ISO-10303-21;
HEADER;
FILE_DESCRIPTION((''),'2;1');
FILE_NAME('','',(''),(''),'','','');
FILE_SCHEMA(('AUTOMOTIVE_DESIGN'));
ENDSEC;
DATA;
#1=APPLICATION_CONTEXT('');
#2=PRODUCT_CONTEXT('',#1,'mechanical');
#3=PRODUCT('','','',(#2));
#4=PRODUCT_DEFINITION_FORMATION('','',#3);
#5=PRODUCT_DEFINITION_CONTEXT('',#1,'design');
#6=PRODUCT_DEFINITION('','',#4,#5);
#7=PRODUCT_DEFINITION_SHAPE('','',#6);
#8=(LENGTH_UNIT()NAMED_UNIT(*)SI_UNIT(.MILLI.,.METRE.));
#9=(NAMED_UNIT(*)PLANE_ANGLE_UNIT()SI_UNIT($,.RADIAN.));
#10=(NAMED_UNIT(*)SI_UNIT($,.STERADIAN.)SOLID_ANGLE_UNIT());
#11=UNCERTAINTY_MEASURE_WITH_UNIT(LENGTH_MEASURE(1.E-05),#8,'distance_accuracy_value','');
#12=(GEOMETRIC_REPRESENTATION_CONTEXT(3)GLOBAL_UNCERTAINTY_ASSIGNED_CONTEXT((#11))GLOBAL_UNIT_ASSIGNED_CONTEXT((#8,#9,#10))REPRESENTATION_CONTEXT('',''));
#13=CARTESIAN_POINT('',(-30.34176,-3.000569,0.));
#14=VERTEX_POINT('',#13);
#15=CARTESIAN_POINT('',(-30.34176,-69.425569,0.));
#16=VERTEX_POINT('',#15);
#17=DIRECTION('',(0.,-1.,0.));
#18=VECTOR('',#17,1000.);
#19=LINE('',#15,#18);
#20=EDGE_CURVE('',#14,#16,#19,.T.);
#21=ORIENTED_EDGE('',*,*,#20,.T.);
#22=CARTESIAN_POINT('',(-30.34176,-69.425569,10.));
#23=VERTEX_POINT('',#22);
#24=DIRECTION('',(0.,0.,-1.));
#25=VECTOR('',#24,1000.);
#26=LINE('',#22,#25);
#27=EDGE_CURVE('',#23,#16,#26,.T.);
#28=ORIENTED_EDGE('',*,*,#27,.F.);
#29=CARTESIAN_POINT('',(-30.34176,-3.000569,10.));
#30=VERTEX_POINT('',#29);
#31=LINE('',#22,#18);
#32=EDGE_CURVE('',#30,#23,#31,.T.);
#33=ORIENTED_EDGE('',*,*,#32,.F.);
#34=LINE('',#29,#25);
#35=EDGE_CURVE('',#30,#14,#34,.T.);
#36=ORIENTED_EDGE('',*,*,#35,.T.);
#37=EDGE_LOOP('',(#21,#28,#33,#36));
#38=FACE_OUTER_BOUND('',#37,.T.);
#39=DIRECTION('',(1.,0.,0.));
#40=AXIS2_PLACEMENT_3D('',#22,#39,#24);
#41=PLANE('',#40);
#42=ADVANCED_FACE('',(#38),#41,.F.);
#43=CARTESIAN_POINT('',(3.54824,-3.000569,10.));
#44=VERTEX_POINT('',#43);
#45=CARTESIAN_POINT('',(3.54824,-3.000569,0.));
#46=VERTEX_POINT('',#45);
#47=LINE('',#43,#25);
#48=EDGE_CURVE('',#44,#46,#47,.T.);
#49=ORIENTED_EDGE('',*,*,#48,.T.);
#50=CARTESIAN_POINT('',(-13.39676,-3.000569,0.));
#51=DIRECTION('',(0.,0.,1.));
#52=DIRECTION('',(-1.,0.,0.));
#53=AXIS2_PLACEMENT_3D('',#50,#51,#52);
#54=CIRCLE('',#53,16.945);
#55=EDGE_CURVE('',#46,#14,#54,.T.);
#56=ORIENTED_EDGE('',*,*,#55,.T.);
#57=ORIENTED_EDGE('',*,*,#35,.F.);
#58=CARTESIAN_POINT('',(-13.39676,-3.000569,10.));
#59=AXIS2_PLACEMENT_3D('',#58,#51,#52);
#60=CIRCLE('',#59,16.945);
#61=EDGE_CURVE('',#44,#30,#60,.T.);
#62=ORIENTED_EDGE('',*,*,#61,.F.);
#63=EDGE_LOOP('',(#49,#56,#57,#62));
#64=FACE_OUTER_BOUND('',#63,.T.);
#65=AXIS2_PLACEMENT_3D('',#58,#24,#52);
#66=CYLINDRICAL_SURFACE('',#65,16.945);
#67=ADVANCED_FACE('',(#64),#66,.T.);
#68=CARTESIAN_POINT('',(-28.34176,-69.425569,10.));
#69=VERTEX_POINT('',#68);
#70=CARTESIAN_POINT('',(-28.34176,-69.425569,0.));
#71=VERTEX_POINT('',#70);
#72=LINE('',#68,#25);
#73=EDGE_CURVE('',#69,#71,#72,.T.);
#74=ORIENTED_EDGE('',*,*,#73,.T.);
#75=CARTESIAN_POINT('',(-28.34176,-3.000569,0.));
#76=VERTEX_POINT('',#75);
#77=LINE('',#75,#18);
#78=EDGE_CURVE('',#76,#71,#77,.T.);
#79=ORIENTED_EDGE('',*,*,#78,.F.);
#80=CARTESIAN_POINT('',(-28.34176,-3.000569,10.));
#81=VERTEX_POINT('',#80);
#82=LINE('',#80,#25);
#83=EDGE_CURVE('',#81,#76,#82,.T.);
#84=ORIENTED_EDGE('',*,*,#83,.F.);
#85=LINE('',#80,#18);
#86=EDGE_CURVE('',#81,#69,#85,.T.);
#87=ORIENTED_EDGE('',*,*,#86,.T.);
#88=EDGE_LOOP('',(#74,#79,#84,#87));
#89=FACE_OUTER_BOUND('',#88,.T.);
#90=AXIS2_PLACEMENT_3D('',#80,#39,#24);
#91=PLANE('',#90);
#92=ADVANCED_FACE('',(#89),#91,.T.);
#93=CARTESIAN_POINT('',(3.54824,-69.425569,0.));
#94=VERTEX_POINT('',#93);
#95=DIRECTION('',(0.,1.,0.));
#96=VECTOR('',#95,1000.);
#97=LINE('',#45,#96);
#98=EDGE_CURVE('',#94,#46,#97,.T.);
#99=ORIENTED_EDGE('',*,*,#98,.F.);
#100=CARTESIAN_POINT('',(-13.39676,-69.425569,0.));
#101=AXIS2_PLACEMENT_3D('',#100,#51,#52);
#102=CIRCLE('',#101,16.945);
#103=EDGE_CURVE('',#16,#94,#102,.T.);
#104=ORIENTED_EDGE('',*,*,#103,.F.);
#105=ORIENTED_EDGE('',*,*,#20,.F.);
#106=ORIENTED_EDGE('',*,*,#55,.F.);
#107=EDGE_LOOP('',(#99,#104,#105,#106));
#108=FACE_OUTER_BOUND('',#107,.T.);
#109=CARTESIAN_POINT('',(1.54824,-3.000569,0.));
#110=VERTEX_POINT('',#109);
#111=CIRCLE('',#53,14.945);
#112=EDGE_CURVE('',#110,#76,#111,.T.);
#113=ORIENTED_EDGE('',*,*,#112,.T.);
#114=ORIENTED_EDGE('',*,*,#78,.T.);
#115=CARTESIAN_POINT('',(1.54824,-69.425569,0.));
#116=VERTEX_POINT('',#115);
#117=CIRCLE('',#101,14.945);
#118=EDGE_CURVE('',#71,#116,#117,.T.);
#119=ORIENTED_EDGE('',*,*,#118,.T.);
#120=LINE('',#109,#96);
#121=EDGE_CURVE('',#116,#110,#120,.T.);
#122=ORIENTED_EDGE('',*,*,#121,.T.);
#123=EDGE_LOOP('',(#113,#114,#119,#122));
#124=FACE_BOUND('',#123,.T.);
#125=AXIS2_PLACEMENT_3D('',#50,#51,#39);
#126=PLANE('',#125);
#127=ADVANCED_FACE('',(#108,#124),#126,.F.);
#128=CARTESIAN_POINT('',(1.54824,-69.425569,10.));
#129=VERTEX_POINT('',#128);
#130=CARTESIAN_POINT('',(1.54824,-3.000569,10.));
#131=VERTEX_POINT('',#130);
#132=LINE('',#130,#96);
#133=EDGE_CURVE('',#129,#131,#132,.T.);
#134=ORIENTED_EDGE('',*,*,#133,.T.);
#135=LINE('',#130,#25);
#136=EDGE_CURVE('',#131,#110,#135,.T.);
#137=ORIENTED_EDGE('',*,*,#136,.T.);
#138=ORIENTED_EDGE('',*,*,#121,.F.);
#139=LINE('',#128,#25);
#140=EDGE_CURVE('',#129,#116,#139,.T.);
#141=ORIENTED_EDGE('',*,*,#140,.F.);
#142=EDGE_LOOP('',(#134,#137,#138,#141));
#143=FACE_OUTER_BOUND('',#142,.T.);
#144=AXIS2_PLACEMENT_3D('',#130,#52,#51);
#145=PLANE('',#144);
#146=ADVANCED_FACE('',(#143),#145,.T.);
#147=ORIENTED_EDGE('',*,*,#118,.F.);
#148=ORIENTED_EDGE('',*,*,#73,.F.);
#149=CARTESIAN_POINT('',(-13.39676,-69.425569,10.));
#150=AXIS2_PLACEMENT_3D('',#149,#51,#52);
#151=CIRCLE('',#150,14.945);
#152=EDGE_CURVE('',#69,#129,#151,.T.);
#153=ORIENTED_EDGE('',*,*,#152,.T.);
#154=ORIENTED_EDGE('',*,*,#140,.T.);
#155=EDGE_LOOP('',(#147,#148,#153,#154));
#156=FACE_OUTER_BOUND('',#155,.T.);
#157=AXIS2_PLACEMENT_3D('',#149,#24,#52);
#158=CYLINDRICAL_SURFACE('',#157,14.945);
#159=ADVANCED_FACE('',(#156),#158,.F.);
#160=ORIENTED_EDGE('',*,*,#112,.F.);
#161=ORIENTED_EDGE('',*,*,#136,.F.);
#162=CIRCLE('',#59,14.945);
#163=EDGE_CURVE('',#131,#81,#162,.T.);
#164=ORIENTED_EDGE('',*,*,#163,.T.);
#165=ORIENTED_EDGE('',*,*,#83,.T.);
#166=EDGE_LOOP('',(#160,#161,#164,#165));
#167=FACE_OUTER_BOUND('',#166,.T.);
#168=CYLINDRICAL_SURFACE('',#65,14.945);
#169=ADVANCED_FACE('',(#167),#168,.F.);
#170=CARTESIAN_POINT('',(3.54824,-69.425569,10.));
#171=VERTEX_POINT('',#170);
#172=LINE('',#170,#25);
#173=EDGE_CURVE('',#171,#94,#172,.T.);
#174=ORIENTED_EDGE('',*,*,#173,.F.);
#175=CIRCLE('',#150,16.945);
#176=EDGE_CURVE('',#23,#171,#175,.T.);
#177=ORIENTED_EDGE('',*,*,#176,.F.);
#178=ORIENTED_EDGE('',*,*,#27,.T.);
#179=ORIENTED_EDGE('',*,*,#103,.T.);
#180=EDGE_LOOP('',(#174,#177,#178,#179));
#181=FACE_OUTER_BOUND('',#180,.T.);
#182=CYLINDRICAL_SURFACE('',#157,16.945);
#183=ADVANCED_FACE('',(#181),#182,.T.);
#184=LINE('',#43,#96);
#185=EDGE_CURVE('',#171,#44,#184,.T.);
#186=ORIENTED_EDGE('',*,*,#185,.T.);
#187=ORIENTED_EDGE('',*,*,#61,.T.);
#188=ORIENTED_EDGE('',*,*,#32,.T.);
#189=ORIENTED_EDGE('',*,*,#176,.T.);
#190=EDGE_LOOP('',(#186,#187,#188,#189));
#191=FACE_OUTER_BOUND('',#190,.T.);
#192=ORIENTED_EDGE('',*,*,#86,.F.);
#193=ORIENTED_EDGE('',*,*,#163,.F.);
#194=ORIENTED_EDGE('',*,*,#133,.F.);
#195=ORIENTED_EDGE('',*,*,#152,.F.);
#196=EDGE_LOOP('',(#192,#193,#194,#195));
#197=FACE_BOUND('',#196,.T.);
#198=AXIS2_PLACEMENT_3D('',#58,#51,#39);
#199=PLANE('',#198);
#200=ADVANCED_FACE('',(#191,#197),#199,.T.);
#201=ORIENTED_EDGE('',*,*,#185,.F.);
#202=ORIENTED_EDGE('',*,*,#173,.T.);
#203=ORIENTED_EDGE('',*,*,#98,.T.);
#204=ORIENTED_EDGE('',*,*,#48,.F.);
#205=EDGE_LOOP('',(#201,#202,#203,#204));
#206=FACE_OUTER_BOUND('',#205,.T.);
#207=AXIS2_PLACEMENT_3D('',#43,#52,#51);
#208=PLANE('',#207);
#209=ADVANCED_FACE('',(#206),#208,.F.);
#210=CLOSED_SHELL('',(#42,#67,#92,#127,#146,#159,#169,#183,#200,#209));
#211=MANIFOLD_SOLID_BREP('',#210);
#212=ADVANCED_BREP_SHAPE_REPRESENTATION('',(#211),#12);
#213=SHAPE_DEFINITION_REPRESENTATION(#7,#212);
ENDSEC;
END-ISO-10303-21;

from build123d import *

# Parameters (mm, degrees)
EXTRUDE_THIN1_DEPTH = 10


with BuildPart() as part:
    # Sketch2 → Extrude-Thin1 (new body)
    with BuildSketch(Plane.XY):
        with BuildLine():
            Line((-30.341760221, -69.425568872), (-30.341760221, -3.000568872))
            ThreePointArc((-30.341760221, -3.000568872), (-13.396760221, 13.944431128), (3.548239779, -3.000568872))
            Line((3.548239779, -3.000568872), (3.548239779, -69.425568872))
            ThreePointArc((3.548239779, -69.425568872), (-13.396760221, -86.370568872), (-30.341760221, -69.425568872))
        make_face()
        with BuildLine():
            Line((-28.341760221, -69.425568872), (-28.341760221, -3.000568872))
            ThreePointArc((-28.341760221, -3.000568872), (-13.396760221, 11.944431128), (1.548239779, -3.000568872))
            Line((1.548239779, -3.000568872), (1.548239779, -69.425568872))
            ThreePointArc((1.548239779, -69.425568872), (-13.396760221, -84.370568872), (-28.341760221, -69.425568872))
        make_face(mode=Mode.SUBTRACT)
    extrude(amount=EXTRUDE_THIN1_DEPTH)


solid = part.part
